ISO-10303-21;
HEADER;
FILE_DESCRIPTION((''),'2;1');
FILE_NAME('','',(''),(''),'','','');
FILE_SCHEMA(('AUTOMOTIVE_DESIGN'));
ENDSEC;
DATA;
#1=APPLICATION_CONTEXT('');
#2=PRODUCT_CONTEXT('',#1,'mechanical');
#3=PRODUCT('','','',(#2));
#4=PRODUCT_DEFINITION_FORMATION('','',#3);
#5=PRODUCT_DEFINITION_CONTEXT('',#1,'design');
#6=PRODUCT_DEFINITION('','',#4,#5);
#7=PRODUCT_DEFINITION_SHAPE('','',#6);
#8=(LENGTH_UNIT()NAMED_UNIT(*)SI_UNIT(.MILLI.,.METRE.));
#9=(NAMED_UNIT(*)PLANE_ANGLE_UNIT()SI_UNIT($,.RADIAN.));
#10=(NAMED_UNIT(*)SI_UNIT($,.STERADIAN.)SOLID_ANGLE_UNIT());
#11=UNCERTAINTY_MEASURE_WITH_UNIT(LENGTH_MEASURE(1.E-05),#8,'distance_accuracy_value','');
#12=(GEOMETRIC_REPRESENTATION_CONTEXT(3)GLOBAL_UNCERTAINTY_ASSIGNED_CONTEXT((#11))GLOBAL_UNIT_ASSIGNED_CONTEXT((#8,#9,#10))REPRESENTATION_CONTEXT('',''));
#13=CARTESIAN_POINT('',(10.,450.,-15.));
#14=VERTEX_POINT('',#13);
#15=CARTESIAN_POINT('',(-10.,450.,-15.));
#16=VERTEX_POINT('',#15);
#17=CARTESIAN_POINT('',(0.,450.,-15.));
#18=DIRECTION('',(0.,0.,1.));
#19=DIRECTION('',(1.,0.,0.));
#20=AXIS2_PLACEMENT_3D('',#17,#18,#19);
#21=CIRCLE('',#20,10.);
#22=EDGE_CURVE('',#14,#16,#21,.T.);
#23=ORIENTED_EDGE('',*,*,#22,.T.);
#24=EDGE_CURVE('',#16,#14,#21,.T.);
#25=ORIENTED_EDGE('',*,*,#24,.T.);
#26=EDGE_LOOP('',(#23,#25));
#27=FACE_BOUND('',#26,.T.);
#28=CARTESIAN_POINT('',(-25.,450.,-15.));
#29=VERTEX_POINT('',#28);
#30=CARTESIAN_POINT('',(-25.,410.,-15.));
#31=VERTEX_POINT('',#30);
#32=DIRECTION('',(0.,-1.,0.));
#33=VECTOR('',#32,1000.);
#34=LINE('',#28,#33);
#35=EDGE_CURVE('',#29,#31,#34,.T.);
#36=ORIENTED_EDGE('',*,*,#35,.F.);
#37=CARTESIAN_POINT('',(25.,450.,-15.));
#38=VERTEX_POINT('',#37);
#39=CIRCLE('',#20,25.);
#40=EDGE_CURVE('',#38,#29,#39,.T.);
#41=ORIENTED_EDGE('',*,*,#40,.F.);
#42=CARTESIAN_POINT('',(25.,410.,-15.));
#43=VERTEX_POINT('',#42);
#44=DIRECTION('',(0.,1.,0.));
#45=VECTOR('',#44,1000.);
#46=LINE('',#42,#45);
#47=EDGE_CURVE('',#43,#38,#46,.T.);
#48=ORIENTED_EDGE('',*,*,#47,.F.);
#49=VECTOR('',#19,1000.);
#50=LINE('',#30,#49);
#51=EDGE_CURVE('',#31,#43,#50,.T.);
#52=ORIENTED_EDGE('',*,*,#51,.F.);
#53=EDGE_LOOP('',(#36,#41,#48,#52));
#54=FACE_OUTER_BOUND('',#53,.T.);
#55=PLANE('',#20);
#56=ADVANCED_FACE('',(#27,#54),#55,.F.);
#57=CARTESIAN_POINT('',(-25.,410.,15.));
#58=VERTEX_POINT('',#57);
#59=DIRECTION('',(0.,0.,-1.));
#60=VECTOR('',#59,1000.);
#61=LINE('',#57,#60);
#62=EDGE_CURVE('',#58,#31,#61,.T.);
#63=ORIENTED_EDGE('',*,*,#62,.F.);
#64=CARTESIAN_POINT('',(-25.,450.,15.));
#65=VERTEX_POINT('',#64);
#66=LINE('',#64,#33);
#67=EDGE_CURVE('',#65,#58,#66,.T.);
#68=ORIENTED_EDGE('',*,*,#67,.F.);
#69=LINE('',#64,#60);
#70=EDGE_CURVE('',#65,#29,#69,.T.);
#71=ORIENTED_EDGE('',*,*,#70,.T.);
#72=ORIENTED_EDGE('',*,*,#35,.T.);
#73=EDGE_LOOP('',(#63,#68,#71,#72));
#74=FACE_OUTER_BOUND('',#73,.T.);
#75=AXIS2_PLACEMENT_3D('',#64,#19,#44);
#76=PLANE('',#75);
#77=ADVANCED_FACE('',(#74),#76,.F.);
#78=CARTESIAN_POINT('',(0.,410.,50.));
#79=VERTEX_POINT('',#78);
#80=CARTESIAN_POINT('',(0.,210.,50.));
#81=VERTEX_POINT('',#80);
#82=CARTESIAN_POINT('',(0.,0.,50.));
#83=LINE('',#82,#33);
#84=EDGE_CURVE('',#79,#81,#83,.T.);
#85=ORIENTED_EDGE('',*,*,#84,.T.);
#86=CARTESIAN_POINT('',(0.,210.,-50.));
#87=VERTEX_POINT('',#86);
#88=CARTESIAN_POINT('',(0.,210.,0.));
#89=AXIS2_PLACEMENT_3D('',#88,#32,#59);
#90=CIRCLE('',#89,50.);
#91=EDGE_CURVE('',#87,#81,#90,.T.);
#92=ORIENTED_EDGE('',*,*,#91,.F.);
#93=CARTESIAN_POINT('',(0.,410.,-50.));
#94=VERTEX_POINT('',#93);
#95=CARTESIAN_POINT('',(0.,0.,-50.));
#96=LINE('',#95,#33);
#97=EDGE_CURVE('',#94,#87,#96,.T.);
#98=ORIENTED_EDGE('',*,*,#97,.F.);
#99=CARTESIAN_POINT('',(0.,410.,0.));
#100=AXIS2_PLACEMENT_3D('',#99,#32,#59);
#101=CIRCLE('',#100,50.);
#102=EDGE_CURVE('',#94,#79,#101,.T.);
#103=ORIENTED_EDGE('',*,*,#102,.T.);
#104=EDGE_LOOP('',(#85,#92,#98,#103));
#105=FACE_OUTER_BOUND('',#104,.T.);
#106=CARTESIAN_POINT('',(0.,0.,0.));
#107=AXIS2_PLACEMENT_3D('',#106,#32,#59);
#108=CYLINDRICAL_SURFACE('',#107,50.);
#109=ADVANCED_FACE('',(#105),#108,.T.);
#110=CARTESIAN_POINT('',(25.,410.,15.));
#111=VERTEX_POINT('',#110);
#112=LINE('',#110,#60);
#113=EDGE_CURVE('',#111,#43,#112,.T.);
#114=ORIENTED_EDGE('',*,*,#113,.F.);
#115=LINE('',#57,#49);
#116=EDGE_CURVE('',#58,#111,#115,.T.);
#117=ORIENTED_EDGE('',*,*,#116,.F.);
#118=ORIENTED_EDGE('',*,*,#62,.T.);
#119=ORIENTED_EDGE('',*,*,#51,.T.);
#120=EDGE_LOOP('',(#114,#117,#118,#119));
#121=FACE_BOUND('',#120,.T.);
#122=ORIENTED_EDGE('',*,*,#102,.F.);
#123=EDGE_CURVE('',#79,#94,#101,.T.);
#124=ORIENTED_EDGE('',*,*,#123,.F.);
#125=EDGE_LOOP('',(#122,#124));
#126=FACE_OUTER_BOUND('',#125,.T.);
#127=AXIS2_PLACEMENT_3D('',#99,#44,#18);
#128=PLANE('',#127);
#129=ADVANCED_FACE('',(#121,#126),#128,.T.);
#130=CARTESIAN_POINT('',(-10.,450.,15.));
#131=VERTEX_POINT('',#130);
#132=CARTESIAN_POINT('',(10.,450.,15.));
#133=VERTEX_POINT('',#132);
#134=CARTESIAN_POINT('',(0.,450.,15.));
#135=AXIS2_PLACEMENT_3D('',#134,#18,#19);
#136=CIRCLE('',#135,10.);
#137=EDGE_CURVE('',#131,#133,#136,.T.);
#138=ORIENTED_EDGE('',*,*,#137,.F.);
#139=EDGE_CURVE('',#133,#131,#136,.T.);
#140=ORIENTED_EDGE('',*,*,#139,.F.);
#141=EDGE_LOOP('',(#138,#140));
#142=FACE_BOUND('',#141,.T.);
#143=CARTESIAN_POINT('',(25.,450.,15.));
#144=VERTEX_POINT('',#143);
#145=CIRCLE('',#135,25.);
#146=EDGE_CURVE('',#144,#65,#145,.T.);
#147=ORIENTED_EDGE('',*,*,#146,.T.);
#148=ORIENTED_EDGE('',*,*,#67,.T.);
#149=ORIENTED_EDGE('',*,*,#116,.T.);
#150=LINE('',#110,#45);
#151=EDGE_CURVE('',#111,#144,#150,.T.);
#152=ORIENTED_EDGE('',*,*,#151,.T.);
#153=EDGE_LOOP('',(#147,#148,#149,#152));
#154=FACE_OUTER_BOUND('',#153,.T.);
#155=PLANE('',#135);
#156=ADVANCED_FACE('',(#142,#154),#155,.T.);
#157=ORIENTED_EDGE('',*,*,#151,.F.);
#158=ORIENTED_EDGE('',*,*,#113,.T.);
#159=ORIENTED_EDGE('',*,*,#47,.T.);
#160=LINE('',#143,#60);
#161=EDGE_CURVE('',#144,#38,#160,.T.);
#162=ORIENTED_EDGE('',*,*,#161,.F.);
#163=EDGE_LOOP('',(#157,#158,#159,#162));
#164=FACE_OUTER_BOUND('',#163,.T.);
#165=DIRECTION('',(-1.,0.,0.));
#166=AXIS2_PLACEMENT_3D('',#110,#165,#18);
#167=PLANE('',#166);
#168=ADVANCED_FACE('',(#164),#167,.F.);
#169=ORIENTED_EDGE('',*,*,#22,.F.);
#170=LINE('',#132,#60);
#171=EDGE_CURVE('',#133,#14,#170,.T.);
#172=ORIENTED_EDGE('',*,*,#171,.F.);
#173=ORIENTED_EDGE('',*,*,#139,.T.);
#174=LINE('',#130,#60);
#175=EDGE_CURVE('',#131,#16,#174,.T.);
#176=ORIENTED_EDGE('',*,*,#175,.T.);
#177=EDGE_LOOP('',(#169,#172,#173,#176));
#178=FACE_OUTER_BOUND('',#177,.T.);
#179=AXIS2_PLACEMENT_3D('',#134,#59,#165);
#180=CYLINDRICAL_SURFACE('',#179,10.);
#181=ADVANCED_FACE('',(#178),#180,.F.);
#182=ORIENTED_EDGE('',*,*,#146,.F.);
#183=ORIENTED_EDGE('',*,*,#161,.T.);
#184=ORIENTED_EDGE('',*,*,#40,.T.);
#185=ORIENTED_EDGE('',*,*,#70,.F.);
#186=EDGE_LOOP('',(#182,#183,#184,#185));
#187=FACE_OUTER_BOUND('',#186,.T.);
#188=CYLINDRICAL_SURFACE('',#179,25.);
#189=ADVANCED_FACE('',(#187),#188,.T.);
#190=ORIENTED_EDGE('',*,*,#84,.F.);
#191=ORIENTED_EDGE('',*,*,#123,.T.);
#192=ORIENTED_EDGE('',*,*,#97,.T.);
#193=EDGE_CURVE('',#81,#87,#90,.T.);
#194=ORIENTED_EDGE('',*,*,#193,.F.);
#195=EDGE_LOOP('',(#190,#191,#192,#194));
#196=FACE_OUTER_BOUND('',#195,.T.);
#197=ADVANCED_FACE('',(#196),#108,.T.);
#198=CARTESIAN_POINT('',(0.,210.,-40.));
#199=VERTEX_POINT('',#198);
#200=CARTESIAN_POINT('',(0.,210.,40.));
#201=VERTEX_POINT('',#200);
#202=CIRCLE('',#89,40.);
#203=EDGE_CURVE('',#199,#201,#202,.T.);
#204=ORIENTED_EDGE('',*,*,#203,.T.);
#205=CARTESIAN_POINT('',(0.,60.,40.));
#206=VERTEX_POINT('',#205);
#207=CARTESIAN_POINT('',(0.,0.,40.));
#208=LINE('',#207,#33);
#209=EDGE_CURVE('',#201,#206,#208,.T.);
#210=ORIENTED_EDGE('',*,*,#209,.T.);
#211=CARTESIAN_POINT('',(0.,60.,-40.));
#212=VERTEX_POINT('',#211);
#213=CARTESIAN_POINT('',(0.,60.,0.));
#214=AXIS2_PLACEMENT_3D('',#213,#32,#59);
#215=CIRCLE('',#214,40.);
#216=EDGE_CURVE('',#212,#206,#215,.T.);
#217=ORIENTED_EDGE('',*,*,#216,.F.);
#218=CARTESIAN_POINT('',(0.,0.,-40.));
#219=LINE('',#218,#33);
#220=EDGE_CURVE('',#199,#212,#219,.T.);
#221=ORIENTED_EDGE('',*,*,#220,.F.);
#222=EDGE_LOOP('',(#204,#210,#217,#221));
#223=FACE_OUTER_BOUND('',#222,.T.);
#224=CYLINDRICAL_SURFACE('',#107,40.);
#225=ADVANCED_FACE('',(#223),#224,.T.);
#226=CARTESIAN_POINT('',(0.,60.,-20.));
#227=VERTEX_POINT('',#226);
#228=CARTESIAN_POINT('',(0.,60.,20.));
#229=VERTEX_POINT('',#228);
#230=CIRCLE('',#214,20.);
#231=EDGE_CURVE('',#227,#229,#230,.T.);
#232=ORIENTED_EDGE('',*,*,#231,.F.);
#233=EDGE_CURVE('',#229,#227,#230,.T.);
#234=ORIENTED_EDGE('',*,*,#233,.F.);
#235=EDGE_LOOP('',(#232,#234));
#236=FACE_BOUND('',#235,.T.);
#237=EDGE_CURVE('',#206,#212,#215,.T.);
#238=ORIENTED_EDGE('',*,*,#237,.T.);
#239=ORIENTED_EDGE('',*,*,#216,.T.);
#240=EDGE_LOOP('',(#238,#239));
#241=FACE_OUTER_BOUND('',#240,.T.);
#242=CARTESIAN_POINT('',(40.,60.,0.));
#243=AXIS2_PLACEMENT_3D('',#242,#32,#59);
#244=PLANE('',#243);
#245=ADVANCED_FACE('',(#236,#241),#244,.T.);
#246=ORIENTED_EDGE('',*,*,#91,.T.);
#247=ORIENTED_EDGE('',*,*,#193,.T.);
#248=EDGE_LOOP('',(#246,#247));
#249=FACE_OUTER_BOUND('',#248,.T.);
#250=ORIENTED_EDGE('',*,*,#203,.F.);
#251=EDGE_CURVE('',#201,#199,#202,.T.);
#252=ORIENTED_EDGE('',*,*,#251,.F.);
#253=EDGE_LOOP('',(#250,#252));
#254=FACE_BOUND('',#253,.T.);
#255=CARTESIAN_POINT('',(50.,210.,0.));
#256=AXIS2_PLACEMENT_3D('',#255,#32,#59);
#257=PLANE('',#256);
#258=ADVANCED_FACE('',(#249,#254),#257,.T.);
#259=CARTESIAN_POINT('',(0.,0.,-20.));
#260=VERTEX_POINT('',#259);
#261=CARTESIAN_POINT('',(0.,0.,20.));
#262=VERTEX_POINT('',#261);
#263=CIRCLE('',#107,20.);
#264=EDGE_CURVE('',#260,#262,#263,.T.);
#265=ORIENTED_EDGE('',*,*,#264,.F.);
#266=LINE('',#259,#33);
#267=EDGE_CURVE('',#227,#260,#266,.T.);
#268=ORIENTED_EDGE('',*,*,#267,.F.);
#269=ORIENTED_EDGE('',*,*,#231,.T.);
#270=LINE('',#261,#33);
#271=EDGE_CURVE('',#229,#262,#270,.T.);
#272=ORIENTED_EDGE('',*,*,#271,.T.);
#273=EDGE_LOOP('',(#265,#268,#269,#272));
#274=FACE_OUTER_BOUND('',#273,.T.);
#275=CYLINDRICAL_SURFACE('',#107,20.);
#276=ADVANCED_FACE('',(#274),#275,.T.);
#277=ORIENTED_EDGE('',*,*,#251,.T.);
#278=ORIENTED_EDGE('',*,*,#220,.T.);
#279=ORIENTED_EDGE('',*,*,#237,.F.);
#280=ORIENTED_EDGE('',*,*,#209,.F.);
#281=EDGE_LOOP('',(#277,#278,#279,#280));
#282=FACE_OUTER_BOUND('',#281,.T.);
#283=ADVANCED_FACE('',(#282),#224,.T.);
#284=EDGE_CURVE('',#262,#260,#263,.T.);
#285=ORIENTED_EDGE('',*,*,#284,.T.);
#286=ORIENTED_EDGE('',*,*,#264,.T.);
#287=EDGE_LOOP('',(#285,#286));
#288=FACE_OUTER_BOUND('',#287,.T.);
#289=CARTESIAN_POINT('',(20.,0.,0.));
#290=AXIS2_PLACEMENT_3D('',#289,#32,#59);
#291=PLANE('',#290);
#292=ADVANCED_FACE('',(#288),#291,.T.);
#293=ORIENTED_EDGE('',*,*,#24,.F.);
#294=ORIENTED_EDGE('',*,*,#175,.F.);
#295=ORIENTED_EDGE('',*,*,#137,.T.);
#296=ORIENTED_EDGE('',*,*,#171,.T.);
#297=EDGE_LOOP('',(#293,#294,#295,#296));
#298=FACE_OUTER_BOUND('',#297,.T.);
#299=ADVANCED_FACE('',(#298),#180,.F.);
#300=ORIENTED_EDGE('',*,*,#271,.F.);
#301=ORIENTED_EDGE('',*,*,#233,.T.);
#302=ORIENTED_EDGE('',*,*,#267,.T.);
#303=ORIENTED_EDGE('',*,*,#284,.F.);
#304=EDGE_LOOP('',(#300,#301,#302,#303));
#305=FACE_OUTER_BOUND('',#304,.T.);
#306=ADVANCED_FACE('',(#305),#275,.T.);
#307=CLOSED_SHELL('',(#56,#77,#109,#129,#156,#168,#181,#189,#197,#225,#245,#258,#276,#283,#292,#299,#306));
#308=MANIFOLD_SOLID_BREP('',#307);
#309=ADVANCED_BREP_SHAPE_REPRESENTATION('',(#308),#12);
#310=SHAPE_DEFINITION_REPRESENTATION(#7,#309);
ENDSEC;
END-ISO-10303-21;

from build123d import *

# Parameters (mm, degrees)
SKETCH2_R           = 10
BOSS_EXTRUDE1_DEPTH = 15


with BuildPart() as part:
    # Sketch1 → Revolve1 (revolve)
    with BuildSketch(Plane.XY, mode=Mode.PRIVATE) as revolve1_sk:
        Polygon((0, 0), (0, 410), (50, 410), (50, 210), (40, 210), (40, 60), (20, 60), (20, 0), align=None)
    revolve(revolve1_sk.sketch.rotate(Axis((0, 0, 0), (0, 1, 0)), 90), axis=Axis((0, 0, 0), (0, 1, 0)))

    # Sketch2 → Boss-Extrude1 (add, symmetric)
    with BuildSketch(Plane.XY):
        with BuildLine():
            Line((-25, 450), (-25, 410))
            Line((-25, 410), (25, 410))
            Line((25, 410), (25, 450))
            ThreePointArc((25, 450), (0, 475), (-25, 450))
        make_face()
        with Locations((0, 450)):
            Circle(SKETCH2_R, mode=Mode.SUBTRACT)
    extrude(amount=BOSS_EXTRUDE1_DEPTH, both=True)


solid = part.part
